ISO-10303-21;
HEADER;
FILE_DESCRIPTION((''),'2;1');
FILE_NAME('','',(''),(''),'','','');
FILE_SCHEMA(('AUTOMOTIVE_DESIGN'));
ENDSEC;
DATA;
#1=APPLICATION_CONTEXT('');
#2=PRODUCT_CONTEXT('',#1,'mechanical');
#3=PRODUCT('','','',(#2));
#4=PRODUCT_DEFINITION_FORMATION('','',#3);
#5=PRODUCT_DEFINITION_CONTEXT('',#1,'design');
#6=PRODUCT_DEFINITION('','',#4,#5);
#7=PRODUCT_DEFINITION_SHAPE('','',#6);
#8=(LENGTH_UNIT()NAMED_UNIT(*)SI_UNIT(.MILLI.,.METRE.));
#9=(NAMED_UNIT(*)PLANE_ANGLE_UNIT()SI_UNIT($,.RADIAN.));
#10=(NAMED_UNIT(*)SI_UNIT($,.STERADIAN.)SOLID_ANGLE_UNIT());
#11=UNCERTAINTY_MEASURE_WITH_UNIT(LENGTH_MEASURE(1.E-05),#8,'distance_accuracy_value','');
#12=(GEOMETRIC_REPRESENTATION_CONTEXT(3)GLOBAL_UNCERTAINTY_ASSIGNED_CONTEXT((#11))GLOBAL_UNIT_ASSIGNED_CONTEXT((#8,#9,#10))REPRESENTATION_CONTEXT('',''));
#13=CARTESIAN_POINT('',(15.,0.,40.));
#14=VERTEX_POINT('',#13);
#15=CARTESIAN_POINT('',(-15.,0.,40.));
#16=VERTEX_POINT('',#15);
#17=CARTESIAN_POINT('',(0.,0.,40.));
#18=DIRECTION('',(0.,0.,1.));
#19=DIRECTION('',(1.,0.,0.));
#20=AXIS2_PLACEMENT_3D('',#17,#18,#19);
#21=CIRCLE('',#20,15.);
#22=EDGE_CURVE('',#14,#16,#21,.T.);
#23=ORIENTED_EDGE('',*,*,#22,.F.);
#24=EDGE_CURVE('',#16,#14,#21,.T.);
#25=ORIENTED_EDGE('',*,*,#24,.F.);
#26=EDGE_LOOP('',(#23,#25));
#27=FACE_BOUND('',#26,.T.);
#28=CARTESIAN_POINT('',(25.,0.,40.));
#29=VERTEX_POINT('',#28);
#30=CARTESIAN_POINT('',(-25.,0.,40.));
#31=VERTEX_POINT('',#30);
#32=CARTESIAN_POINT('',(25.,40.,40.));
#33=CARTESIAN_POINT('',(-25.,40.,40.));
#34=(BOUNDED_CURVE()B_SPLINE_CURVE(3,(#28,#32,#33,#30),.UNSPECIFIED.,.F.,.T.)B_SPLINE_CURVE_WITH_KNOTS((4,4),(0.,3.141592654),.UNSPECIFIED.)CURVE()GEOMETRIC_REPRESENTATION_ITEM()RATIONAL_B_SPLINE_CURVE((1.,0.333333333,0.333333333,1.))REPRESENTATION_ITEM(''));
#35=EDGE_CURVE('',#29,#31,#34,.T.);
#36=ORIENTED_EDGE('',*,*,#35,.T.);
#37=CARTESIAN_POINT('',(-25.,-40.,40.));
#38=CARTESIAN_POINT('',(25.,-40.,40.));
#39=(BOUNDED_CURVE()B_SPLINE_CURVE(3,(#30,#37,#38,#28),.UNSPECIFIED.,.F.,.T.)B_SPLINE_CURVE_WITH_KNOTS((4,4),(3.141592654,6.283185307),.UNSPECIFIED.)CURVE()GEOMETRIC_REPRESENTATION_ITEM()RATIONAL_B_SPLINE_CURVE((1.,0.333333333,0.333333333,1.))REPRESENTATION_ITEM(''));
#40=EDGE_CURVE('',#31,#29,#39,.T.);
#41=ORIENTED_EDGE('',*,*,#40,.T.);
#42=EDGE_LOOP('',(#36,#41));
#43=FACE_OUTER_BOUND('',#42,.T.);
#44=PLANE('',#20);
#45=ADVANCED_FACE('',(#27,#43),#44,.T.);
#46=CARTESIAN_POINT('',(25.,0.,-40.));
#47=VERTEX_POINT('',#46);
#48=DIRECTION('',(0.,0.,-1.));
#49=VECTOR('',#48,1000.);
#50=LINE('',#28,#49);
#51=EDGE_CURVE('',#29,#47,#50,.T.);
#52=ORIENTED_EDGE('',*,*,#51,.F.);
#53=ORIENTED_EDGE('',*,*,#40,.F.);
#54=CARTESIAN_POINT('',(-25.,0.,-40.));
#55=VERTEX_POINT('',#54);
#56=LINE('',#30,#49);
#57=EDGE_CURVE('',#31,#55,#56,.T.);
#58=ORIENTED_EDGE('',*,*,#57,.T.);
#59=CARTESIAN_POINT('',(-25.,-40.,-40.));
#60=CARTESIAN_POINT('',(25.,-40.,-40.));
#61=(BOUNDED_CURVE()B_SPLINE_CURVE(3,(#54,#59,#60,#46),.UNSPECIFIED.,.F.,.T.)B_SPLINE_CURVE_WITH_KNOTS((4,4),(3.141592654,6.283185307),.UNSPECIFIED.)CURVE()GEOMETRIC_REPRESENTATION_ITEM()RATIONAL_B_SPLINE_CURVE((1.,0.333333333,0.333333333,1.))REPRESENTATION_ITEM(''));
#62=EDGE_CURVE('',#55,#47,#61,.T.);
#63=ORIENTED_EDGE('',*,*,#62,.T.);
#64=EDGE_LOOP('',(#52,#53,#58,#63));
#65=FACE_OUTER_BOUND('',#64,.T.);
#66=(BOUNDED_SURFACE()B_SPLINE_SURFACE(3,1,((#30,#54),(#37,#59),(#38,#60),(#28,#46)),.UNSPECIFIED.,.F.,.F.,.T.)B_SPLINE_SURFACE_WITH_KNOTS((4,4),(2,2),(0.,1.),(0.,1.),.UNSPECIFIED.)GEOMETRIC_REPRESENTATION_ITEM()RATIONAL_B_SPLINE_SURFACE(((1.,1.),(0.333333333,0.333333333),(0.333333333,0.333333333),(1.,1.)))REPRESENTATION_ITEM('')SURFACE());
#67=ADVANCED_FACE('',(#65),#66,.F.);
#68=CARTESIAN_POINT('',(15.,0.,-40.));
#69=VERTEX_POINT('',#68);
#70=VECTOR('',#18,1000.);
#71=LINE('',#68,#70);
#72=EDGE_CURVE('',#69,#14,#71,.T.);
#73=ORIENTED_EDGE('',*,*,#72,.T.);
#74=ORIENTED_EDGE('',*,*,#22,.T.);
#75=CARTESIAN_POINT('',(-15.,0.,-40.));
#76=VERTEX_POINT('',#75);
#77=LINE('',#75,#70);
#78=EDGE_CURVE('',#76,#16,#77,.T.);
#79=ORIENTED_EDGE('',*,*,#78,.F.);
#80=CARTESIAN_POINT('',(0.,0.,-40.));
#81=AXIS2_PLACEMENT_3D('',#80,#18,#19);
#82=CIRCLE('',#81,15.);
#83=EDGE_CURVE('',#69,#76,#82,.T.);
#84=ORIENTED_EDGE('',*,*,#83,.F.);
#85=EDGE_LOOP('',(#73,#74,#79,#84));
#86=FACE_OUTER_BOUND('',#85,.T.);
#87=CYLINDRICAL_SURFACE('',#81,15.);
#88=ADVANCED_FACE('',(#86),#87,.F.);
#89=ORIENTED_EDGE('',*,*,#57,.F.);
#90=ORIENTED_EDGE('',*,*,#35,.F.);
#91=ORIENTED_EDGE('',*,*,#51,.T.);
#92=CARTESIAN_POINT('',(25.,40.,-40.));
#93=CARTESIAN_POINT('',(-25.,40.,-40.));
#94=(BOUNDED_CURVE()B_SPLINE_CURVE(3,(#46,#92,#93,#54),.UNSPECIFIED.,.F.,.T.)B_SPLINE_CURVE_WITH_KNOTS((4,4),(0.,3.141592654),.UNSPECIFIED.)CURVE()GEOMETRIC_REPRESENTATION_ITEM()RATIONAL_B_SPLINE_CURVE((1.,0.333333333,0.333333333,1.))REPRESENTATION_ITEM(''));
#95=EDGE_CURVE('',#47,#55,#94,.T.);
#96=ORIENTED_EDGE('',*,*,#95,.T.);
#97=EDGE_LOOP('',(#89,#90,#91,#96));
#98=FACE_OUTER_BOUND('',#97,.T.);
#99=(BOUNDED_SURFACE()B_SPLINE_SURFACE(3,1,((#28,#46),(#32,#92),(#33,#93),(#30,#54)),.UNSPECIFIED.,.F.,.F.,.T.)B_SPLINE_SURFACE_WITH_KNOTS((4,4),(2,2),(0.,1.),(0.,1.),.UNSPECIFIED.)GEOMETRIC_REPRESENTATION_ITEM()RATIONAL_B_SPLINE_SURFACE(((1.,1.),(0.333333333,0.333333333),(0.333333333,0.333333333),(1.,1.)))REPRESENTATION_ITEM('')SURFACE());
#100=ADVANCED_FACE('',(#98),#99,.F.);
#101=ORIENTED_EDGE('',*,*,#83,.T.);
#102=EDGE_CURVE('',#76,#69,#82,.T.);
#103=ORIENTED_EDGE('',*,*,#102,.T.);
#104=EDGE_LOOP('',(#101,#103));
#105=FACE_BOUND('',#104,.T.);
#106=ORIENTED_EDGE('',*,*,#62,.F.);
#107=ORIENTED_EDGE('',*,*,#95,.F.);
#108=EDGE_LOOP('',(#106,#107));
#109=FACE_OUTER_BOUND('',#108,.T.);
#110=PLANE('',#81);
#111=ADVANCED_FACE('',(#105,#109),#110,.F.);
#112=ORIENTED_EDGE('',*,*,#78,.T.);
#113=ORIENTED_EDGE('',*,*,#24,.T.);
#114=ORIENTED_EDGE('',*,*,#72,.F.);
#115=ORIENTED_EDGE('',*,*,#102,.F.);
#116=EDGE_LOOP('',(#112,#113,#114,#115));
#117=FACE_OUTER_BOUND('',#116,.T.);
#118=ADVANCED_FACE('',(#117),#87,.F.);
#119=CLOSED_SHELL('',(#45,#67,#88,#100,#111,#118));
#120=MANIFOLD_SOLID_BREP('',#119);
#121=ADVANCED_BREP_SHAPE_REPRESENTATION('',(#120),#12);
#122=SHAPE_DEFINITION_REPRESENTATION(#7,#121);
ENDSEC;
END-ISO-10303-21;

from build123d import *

# Parameters (mm, degrees)
SKETCH1_RX          = 25
SKETCH1_RY          = 20
BOSS_EXTRUDE1_DEPTH = 40
SKETCH2_R           = 15
CUT_EXTRUDE1_DEPTH  = 87.168439698


with BuildPart() as part:
    # Sketch1 → Boss-Extrude1 (new, symmetric)
    with BuildSketch(Plane.XY):
        with Locations((0, 0)):
            Ellipse(SKETCH1_RX, SKETCH1_RY)
    extrude(amount=BOSS_EXTRUDE1_DEPTH, both=True)

    # Sketch2 → Cut-Extrude1 (cut, through all)
    with BuildSketch(Plane.XY.offset(40)):
        Circle(SKETCH2_R)
    extrude(amount=-CUT_EXTRUDE1_DEPTH, mode=Mode.SUBTRACT)


solid = part.part
